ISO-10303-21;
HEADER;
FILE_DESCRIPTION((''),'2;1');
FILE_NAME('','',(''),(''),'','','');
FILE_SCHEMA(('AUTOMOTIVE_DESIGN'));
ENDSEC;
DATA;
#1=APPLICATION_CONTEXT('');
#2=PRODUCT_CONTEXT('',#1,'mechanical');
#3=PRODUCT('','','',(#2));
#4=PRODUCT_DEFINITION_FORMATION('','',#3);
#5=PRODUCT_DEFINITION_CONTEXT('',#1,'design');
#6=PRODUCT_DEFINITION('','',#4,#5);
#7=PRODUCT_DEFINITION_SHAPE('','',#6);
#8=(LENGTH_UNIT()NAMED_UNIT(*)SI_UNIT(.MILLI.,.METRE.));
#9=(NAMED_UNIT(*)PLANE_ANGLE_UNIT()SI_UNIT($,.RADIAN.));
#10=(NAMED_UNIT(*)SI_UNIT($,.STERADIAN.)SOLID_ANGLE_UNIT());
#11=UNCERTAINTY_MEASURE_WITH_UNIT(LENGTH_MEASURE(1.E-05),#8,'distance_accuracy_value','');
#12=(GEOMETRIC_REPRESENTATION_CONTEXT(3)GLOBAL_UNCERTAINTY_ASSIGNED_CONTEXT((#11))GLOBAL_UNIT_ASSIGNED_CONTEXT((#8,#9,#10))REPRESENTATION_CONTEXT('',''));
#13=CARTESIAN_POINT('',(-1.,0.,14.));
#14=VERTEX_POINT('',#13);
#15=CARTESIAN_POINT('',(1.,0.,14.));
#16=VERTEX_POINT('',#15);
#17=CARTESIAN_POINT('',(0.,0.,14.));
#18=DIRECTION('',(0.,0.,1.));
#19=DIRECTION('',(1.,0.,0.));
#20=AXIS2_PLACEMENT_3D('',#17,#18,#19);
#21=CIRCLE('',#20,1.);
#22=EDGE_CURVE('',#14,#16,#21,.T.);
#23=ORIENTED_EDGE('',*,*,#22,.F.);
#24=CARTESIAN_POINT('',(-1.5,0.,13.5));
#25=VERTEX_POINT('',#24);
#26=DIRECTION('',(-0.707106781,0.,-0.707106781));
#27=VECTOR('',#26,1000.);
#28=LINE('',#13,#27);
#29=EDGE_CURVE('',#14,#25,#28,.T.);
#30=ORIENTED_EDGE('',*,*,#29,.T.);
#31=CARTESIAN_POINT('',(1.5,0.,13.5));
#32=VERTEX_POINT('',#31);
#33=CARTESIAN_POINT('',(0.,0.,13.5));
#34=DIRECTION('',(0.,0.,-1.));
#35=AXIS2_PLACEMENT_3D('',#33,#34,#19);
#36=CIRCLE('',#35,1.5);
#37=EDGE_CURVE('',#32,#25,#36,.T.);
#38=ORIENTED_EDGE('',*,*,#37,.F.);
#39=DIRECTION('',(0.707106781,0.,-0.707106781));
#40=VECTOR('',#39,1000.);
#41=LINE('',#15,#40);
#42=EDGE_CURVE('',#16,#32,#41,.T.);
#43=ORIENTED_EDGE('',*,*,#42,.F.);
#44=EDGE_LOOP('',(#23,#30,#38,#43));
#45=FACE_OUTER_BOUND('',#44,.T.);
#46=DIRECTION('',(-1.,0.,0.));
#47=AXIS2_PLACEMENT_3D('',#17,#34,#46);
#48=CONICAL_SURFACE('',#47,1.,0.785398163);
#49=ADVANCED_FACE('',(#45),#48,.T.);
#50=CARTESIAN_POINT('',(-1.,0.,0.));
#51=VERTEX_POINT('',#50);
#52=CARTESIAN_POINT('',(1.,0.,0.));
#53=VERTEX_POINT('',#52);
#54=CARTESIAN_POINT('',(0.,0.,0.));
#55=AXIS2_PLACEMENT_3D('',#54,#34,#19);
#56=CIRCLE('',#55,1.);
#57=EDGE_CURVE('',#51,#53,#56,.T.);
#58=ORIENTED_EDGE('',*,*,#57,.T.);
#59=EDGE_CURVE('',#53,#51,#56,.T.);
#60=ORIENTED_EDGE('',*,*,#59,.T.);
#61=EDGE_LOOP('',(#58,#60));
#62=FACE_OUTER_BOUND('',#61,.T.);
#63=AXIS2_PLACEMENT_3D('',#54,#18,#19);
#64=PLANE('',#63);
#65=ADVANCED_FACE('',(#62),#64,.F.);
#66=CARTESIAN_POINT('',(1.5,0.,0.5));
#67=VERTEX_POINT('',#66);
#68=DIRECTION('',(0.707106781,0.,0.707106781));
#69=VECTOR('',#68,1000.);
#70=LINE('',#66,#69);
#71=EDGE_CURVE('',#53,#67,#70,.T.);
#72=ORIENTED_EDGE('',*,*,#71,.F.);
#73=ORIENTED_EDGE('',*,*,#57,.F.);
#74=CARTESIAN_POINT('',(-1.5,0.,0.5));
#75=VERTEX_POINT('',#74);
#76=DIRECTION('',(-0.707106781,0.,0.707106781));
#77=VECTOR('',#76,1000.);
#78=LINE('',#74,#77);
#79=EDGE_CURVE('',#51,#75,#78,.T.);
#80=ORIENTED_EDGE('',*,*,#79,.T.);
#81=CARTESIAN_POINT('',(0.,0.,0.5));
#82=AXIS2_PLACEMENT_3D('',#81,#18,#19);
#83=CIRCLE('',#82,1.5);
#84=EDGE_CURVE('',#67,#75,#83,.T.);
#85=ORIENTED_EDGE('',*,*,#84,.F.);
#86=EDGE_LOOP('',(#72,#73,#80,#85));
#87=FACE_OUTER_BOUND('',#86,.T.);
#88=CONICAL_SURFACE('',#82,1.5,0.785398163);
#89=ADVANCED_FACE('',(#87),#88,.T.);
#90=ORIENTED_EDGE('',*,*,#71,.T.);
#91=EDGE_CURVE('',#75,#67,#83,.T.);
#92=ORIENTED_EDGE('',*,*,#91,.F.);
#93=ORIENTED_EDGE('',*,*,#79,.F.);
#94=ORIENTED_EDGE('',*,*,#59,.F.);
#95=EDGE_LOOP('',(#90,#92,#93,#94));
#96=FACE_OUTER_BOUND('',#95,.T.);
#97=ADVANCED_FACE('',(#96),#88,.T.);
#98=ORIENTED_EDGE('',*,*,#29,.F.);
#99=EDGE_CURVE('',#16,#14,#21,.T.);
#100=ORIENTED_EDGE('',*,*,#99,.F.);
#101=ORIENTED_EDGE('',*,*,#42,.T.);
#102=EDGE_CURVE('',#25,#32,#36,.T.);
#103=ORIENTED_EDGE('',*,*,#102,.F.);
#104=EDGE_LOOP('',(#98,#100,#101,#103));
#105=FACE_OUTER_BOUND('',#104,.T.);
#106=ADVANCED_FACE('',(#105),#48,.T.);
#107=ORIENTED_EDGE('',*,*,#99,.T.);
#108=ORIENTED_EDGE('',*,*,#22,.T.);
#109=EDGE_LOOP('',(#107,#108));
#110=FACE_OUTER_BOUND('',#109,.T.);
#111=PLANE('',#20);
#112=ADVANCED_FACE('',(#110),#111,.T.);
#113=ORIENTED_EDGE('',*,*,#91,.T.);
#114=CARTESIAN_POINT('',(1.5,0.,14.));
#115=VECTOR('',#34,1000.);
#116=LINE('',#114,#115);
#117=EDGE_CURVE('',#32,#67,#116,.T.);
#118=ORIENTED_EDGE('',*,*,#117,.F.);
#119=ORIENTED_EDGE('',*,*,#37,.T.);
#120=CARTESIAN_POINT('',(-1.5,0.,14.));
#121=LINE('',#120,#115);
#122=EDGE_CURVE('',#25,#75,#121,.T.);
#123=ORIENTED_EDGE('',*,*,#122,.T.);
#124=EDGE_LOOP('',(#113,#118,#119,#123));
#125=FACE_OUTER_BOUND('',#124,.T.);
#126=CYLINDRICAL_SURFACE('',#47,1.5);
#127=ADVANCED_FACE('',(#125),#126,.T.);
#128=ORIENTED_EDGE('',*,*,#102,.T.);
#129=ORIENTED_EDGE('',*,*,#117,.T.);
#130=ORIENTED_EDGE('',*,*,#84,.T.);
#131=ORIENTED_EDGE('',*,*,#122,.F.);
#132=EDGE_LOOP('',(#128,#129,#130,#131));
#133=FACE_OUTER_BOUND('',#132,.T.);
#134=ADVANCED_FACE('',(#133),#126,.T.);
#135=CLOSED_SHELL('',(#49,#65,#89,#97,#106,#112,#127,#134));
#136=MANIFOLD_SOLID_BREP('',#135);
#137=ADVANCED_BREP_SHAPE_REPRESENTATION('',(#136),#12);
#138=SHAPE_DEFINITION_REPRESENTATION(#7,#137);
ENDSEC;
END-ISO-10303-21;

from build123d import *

# Parameters (mm, degrees)
SKETCH1_R           = 1.5
BOSS_EXTRUDE1_DEPTH = 14
CHAMFER1_SIZE       = 0.5


with BuildPart() as part:
    # Sketch1 → Boss-Extrude1 (new body)
    with BuildSketch(Plane.XY):
        Circle(SKETCH1_R)
    extrude(amount=BOSS_EXTRUDE1_DEPTH)

    # Chamfer1
    chamfer1_edges = [part.edges().sort_by_distance(p)[0] for p in [
        (-1.5, 0, 0),
        (-1.5, 0, 14),
    ]]
    chamfer(chamfer1_edges, length=CHAMFER1_SIZE)


solid = part.part
